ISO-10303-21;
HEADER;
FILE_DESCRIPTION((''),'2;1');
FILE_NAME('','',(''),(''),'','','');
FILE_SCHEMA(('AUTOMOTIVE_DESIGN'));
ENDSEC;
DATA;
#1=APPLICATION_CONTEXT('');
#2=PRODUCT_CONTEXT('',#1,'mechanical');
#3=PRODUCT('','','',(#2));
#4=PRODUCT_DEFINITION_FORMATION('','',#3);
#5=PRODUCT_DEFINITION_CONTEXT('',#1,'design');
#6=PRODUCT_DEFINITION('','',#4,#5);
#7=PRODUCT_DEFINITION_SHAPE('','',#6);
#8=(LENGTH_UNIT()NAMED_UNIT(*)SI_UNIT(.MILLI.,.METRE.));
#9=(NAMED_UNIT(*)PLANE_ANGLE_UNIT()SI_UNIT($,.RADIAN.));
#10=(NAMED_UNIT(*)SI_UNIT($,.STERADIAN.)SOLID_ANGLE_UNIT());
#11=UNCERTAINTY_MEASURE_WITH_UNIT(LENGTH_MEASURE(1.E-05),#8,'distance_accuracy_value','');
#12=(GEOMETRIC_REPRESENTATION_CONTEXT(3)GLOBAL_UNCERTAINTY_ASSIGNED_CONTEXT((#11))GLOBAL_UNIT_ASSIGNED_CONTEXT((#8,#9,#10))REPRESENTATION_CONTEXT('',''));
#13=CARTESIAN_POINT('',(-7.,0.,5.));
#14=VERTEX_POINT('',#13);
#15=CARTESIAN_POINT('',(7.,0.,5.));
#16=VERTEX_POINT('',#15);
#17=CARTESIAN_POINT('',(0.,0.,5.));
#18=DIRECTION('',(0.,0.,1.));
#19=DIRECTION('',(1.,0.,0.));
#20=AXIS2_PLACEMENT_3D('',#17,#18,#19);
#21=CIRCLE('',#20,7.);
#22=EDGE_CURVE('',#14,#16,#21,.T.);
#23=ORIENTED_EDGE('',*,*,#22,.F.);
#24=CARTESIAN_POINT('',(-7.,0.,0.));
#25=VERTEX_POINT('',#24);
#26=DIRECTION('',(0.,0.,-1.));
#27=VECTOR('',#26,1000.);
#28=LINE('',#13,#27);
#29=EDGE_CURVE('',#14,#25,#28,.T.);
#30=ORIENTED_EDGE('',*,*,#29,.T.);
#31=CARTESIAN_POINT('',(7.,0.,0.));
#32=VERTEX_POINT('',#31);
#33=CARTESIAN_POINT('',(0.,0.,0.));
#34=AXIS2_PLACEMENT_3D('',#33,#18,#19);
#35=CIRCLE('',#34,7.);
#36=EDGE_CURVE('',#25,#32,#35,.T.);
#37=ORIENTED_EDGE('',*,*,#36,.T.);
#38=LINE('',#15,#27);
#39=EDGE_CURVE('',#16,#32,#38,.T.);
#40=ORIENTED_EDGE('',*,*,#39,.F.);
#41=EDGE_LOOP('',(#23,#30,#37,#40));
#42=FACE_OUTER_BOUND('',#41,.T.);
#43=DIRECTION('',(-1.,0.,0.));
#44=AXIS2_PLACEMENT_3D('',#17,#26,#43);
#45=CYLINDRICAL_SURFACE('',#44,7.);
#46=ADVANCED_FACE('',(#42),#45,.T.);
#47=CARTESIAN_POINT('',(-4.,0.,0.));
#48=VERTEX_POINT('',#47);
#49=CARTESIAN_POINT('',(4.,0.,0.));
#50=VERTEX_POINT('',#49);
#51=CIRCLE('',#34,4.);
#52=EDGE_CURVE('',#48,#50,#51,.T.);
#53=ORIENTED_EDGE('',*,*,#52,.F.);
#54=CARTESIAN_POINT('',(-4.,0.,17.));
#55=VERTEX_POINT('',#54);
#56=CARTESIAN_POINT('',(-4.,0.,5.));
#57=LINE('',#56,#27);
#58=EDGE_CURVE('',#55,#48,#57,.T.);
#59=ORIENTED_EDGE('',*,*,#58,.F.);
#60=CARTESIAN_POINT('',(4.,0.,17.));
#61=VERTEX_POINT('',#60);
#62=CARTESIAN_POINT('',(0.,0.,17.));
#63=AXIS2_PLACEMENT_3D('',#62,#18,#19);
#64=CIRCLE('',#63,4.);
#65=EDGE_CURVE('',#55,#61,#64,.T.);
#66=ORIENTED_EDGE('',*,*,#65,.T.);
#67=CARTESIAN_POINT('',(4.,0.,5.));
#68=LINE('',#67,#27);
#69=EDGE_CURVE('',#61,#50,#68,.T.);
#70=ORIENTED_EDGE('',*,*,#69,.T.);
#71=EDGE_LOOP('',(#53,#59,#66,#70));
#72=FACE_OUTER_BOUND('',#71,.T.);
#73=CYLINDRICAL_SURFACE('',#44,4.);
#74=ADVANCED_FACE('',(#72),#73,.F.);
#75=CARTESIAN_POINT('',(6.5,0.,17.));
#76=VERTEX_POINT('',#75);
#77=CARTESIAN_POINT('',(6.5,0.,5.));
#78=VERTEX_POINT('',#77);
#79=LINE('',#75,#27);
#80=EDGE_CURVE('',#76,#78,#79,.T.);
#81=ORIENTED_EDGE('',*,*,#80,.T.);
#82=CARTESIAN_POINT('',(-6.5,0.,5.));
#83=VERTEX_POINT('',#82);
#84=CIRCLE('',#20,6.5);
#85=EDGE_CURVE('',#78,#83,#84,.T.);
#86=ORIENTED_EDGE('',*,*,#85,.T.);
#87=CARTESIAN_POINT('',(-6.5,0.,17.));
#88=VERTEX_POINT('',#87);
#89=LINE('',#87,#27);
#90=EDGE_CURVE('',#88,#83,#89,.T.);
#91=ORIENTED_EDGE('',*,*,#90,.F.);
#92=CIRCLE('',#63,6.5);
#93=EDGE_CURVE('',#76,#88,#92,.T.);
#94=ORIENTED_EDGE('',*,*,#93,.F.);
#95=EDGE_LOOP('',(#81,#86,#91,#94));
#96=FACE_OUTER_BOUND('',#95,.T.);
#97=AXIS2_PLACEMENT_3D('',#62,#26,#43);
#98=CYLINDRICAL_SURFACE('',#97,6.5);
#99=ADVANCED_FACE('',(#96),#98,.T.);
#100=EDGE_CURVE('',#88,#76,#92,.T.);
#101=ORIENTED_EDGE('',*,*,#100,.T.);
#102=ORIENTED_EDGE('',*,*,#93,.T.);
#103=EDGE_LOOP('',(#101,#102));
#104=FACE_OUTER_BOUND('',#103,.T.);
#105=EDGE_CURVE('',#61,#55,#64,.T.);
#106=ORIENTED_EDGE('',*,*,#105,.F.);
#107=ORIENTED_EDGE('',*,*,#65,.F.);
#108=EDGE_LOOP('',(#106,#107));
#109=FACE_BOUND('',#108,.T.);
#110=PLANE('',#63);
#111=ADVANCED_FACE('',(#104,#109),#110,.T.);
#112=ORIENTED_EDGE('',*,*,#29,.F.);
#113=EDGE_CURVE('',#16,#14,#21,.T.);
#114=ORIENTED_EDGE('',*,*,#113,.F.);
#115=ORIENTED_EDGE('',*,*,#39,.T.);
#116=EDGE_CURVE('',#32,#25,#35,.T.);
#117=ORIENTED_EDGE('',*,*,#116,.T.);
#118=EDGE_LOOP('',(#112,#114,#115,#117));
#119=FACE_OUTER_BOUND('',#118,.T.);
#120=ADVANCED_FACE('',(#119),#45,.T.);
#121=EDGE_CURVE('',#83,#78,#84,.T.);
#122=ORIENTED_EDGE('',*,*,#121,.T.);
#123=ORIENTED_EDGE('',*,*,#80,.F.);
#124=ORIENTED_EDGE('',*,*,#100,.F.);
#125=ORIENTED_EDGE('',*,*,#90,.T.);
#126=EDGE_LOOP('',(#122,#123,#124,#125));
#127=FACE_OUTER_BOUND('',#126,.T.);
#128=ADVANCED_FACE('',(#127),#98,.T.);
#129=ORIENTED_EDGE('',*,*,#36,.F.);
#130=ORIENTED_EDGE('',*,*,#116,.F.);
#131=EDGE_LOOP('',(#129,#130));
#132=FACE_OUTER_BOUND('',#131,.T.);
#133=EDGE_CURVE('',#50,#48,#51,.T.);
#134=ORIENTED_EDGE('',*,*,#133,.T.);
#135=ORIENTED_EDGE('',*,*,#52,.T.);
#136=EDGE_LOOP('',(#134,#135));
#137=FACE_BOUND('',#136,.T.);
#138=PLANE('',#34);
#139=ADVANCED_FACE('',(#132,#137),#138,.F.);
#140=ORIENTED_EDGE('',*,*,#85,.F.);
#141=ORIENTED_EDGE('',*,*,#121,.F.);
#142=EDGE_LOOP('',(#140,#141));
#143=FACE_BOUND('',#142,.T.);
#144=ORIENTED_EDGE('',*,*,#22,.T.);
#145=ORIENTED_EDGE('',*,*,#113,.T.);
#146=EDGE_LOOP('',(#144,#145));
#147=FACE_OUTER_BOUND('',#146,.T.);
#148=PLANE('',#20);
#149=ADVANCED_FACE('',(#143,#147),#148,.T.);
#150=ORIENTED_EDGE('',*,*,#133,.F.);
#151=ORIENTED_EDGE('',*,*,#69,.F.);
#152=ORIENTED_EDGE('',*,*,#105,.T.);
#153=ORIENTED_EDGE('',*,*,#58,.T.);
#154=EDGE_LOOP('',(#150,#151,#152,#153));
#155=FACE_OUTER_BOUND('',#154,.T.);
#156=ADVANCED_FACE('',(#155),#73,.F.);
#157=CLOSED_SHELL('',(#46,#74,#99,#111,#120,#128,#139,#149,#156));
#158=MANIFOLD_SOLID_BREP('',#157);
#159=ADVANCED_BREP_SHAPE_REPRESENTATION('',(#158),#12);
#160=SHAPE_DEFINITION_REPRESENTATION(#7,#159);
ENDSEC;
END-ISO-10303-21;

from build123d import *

# Parameters (mm, degrees)
SKETCH1_R           = 7
SKETCH1_R_2         = 4
BOSS_EXTRUDE1_DEPTH = 5
SKETCH2_R           = 6.5
SKETCH2_R_2         = 4
BOSS_EXTRUDE2_DEPTH = 12


with BuildPart() as part:
    # Sketch1 → Boss-Extrude1 (new body)
    with BuildSketch(Plane.XY):
        Circle(SKETCH1_R)
        Circle(SKETCH1_R_2, mode=Mode.SUBTRACT)
    extrude(amount=BOSS_EXTRUDE1_DEPTH)

    # Sketch2 → Boss-Extrude2 (add)
    with BuildSketch(Plane.XY.offset(5)):
        Circle(SKETCH2_R)
        Circle(SKETCH2_R_2, mode=Mode.SUBTRACT)
    extrude(amount=BOSS_EXTRUDE2_DEPTH)


solid = part.part
